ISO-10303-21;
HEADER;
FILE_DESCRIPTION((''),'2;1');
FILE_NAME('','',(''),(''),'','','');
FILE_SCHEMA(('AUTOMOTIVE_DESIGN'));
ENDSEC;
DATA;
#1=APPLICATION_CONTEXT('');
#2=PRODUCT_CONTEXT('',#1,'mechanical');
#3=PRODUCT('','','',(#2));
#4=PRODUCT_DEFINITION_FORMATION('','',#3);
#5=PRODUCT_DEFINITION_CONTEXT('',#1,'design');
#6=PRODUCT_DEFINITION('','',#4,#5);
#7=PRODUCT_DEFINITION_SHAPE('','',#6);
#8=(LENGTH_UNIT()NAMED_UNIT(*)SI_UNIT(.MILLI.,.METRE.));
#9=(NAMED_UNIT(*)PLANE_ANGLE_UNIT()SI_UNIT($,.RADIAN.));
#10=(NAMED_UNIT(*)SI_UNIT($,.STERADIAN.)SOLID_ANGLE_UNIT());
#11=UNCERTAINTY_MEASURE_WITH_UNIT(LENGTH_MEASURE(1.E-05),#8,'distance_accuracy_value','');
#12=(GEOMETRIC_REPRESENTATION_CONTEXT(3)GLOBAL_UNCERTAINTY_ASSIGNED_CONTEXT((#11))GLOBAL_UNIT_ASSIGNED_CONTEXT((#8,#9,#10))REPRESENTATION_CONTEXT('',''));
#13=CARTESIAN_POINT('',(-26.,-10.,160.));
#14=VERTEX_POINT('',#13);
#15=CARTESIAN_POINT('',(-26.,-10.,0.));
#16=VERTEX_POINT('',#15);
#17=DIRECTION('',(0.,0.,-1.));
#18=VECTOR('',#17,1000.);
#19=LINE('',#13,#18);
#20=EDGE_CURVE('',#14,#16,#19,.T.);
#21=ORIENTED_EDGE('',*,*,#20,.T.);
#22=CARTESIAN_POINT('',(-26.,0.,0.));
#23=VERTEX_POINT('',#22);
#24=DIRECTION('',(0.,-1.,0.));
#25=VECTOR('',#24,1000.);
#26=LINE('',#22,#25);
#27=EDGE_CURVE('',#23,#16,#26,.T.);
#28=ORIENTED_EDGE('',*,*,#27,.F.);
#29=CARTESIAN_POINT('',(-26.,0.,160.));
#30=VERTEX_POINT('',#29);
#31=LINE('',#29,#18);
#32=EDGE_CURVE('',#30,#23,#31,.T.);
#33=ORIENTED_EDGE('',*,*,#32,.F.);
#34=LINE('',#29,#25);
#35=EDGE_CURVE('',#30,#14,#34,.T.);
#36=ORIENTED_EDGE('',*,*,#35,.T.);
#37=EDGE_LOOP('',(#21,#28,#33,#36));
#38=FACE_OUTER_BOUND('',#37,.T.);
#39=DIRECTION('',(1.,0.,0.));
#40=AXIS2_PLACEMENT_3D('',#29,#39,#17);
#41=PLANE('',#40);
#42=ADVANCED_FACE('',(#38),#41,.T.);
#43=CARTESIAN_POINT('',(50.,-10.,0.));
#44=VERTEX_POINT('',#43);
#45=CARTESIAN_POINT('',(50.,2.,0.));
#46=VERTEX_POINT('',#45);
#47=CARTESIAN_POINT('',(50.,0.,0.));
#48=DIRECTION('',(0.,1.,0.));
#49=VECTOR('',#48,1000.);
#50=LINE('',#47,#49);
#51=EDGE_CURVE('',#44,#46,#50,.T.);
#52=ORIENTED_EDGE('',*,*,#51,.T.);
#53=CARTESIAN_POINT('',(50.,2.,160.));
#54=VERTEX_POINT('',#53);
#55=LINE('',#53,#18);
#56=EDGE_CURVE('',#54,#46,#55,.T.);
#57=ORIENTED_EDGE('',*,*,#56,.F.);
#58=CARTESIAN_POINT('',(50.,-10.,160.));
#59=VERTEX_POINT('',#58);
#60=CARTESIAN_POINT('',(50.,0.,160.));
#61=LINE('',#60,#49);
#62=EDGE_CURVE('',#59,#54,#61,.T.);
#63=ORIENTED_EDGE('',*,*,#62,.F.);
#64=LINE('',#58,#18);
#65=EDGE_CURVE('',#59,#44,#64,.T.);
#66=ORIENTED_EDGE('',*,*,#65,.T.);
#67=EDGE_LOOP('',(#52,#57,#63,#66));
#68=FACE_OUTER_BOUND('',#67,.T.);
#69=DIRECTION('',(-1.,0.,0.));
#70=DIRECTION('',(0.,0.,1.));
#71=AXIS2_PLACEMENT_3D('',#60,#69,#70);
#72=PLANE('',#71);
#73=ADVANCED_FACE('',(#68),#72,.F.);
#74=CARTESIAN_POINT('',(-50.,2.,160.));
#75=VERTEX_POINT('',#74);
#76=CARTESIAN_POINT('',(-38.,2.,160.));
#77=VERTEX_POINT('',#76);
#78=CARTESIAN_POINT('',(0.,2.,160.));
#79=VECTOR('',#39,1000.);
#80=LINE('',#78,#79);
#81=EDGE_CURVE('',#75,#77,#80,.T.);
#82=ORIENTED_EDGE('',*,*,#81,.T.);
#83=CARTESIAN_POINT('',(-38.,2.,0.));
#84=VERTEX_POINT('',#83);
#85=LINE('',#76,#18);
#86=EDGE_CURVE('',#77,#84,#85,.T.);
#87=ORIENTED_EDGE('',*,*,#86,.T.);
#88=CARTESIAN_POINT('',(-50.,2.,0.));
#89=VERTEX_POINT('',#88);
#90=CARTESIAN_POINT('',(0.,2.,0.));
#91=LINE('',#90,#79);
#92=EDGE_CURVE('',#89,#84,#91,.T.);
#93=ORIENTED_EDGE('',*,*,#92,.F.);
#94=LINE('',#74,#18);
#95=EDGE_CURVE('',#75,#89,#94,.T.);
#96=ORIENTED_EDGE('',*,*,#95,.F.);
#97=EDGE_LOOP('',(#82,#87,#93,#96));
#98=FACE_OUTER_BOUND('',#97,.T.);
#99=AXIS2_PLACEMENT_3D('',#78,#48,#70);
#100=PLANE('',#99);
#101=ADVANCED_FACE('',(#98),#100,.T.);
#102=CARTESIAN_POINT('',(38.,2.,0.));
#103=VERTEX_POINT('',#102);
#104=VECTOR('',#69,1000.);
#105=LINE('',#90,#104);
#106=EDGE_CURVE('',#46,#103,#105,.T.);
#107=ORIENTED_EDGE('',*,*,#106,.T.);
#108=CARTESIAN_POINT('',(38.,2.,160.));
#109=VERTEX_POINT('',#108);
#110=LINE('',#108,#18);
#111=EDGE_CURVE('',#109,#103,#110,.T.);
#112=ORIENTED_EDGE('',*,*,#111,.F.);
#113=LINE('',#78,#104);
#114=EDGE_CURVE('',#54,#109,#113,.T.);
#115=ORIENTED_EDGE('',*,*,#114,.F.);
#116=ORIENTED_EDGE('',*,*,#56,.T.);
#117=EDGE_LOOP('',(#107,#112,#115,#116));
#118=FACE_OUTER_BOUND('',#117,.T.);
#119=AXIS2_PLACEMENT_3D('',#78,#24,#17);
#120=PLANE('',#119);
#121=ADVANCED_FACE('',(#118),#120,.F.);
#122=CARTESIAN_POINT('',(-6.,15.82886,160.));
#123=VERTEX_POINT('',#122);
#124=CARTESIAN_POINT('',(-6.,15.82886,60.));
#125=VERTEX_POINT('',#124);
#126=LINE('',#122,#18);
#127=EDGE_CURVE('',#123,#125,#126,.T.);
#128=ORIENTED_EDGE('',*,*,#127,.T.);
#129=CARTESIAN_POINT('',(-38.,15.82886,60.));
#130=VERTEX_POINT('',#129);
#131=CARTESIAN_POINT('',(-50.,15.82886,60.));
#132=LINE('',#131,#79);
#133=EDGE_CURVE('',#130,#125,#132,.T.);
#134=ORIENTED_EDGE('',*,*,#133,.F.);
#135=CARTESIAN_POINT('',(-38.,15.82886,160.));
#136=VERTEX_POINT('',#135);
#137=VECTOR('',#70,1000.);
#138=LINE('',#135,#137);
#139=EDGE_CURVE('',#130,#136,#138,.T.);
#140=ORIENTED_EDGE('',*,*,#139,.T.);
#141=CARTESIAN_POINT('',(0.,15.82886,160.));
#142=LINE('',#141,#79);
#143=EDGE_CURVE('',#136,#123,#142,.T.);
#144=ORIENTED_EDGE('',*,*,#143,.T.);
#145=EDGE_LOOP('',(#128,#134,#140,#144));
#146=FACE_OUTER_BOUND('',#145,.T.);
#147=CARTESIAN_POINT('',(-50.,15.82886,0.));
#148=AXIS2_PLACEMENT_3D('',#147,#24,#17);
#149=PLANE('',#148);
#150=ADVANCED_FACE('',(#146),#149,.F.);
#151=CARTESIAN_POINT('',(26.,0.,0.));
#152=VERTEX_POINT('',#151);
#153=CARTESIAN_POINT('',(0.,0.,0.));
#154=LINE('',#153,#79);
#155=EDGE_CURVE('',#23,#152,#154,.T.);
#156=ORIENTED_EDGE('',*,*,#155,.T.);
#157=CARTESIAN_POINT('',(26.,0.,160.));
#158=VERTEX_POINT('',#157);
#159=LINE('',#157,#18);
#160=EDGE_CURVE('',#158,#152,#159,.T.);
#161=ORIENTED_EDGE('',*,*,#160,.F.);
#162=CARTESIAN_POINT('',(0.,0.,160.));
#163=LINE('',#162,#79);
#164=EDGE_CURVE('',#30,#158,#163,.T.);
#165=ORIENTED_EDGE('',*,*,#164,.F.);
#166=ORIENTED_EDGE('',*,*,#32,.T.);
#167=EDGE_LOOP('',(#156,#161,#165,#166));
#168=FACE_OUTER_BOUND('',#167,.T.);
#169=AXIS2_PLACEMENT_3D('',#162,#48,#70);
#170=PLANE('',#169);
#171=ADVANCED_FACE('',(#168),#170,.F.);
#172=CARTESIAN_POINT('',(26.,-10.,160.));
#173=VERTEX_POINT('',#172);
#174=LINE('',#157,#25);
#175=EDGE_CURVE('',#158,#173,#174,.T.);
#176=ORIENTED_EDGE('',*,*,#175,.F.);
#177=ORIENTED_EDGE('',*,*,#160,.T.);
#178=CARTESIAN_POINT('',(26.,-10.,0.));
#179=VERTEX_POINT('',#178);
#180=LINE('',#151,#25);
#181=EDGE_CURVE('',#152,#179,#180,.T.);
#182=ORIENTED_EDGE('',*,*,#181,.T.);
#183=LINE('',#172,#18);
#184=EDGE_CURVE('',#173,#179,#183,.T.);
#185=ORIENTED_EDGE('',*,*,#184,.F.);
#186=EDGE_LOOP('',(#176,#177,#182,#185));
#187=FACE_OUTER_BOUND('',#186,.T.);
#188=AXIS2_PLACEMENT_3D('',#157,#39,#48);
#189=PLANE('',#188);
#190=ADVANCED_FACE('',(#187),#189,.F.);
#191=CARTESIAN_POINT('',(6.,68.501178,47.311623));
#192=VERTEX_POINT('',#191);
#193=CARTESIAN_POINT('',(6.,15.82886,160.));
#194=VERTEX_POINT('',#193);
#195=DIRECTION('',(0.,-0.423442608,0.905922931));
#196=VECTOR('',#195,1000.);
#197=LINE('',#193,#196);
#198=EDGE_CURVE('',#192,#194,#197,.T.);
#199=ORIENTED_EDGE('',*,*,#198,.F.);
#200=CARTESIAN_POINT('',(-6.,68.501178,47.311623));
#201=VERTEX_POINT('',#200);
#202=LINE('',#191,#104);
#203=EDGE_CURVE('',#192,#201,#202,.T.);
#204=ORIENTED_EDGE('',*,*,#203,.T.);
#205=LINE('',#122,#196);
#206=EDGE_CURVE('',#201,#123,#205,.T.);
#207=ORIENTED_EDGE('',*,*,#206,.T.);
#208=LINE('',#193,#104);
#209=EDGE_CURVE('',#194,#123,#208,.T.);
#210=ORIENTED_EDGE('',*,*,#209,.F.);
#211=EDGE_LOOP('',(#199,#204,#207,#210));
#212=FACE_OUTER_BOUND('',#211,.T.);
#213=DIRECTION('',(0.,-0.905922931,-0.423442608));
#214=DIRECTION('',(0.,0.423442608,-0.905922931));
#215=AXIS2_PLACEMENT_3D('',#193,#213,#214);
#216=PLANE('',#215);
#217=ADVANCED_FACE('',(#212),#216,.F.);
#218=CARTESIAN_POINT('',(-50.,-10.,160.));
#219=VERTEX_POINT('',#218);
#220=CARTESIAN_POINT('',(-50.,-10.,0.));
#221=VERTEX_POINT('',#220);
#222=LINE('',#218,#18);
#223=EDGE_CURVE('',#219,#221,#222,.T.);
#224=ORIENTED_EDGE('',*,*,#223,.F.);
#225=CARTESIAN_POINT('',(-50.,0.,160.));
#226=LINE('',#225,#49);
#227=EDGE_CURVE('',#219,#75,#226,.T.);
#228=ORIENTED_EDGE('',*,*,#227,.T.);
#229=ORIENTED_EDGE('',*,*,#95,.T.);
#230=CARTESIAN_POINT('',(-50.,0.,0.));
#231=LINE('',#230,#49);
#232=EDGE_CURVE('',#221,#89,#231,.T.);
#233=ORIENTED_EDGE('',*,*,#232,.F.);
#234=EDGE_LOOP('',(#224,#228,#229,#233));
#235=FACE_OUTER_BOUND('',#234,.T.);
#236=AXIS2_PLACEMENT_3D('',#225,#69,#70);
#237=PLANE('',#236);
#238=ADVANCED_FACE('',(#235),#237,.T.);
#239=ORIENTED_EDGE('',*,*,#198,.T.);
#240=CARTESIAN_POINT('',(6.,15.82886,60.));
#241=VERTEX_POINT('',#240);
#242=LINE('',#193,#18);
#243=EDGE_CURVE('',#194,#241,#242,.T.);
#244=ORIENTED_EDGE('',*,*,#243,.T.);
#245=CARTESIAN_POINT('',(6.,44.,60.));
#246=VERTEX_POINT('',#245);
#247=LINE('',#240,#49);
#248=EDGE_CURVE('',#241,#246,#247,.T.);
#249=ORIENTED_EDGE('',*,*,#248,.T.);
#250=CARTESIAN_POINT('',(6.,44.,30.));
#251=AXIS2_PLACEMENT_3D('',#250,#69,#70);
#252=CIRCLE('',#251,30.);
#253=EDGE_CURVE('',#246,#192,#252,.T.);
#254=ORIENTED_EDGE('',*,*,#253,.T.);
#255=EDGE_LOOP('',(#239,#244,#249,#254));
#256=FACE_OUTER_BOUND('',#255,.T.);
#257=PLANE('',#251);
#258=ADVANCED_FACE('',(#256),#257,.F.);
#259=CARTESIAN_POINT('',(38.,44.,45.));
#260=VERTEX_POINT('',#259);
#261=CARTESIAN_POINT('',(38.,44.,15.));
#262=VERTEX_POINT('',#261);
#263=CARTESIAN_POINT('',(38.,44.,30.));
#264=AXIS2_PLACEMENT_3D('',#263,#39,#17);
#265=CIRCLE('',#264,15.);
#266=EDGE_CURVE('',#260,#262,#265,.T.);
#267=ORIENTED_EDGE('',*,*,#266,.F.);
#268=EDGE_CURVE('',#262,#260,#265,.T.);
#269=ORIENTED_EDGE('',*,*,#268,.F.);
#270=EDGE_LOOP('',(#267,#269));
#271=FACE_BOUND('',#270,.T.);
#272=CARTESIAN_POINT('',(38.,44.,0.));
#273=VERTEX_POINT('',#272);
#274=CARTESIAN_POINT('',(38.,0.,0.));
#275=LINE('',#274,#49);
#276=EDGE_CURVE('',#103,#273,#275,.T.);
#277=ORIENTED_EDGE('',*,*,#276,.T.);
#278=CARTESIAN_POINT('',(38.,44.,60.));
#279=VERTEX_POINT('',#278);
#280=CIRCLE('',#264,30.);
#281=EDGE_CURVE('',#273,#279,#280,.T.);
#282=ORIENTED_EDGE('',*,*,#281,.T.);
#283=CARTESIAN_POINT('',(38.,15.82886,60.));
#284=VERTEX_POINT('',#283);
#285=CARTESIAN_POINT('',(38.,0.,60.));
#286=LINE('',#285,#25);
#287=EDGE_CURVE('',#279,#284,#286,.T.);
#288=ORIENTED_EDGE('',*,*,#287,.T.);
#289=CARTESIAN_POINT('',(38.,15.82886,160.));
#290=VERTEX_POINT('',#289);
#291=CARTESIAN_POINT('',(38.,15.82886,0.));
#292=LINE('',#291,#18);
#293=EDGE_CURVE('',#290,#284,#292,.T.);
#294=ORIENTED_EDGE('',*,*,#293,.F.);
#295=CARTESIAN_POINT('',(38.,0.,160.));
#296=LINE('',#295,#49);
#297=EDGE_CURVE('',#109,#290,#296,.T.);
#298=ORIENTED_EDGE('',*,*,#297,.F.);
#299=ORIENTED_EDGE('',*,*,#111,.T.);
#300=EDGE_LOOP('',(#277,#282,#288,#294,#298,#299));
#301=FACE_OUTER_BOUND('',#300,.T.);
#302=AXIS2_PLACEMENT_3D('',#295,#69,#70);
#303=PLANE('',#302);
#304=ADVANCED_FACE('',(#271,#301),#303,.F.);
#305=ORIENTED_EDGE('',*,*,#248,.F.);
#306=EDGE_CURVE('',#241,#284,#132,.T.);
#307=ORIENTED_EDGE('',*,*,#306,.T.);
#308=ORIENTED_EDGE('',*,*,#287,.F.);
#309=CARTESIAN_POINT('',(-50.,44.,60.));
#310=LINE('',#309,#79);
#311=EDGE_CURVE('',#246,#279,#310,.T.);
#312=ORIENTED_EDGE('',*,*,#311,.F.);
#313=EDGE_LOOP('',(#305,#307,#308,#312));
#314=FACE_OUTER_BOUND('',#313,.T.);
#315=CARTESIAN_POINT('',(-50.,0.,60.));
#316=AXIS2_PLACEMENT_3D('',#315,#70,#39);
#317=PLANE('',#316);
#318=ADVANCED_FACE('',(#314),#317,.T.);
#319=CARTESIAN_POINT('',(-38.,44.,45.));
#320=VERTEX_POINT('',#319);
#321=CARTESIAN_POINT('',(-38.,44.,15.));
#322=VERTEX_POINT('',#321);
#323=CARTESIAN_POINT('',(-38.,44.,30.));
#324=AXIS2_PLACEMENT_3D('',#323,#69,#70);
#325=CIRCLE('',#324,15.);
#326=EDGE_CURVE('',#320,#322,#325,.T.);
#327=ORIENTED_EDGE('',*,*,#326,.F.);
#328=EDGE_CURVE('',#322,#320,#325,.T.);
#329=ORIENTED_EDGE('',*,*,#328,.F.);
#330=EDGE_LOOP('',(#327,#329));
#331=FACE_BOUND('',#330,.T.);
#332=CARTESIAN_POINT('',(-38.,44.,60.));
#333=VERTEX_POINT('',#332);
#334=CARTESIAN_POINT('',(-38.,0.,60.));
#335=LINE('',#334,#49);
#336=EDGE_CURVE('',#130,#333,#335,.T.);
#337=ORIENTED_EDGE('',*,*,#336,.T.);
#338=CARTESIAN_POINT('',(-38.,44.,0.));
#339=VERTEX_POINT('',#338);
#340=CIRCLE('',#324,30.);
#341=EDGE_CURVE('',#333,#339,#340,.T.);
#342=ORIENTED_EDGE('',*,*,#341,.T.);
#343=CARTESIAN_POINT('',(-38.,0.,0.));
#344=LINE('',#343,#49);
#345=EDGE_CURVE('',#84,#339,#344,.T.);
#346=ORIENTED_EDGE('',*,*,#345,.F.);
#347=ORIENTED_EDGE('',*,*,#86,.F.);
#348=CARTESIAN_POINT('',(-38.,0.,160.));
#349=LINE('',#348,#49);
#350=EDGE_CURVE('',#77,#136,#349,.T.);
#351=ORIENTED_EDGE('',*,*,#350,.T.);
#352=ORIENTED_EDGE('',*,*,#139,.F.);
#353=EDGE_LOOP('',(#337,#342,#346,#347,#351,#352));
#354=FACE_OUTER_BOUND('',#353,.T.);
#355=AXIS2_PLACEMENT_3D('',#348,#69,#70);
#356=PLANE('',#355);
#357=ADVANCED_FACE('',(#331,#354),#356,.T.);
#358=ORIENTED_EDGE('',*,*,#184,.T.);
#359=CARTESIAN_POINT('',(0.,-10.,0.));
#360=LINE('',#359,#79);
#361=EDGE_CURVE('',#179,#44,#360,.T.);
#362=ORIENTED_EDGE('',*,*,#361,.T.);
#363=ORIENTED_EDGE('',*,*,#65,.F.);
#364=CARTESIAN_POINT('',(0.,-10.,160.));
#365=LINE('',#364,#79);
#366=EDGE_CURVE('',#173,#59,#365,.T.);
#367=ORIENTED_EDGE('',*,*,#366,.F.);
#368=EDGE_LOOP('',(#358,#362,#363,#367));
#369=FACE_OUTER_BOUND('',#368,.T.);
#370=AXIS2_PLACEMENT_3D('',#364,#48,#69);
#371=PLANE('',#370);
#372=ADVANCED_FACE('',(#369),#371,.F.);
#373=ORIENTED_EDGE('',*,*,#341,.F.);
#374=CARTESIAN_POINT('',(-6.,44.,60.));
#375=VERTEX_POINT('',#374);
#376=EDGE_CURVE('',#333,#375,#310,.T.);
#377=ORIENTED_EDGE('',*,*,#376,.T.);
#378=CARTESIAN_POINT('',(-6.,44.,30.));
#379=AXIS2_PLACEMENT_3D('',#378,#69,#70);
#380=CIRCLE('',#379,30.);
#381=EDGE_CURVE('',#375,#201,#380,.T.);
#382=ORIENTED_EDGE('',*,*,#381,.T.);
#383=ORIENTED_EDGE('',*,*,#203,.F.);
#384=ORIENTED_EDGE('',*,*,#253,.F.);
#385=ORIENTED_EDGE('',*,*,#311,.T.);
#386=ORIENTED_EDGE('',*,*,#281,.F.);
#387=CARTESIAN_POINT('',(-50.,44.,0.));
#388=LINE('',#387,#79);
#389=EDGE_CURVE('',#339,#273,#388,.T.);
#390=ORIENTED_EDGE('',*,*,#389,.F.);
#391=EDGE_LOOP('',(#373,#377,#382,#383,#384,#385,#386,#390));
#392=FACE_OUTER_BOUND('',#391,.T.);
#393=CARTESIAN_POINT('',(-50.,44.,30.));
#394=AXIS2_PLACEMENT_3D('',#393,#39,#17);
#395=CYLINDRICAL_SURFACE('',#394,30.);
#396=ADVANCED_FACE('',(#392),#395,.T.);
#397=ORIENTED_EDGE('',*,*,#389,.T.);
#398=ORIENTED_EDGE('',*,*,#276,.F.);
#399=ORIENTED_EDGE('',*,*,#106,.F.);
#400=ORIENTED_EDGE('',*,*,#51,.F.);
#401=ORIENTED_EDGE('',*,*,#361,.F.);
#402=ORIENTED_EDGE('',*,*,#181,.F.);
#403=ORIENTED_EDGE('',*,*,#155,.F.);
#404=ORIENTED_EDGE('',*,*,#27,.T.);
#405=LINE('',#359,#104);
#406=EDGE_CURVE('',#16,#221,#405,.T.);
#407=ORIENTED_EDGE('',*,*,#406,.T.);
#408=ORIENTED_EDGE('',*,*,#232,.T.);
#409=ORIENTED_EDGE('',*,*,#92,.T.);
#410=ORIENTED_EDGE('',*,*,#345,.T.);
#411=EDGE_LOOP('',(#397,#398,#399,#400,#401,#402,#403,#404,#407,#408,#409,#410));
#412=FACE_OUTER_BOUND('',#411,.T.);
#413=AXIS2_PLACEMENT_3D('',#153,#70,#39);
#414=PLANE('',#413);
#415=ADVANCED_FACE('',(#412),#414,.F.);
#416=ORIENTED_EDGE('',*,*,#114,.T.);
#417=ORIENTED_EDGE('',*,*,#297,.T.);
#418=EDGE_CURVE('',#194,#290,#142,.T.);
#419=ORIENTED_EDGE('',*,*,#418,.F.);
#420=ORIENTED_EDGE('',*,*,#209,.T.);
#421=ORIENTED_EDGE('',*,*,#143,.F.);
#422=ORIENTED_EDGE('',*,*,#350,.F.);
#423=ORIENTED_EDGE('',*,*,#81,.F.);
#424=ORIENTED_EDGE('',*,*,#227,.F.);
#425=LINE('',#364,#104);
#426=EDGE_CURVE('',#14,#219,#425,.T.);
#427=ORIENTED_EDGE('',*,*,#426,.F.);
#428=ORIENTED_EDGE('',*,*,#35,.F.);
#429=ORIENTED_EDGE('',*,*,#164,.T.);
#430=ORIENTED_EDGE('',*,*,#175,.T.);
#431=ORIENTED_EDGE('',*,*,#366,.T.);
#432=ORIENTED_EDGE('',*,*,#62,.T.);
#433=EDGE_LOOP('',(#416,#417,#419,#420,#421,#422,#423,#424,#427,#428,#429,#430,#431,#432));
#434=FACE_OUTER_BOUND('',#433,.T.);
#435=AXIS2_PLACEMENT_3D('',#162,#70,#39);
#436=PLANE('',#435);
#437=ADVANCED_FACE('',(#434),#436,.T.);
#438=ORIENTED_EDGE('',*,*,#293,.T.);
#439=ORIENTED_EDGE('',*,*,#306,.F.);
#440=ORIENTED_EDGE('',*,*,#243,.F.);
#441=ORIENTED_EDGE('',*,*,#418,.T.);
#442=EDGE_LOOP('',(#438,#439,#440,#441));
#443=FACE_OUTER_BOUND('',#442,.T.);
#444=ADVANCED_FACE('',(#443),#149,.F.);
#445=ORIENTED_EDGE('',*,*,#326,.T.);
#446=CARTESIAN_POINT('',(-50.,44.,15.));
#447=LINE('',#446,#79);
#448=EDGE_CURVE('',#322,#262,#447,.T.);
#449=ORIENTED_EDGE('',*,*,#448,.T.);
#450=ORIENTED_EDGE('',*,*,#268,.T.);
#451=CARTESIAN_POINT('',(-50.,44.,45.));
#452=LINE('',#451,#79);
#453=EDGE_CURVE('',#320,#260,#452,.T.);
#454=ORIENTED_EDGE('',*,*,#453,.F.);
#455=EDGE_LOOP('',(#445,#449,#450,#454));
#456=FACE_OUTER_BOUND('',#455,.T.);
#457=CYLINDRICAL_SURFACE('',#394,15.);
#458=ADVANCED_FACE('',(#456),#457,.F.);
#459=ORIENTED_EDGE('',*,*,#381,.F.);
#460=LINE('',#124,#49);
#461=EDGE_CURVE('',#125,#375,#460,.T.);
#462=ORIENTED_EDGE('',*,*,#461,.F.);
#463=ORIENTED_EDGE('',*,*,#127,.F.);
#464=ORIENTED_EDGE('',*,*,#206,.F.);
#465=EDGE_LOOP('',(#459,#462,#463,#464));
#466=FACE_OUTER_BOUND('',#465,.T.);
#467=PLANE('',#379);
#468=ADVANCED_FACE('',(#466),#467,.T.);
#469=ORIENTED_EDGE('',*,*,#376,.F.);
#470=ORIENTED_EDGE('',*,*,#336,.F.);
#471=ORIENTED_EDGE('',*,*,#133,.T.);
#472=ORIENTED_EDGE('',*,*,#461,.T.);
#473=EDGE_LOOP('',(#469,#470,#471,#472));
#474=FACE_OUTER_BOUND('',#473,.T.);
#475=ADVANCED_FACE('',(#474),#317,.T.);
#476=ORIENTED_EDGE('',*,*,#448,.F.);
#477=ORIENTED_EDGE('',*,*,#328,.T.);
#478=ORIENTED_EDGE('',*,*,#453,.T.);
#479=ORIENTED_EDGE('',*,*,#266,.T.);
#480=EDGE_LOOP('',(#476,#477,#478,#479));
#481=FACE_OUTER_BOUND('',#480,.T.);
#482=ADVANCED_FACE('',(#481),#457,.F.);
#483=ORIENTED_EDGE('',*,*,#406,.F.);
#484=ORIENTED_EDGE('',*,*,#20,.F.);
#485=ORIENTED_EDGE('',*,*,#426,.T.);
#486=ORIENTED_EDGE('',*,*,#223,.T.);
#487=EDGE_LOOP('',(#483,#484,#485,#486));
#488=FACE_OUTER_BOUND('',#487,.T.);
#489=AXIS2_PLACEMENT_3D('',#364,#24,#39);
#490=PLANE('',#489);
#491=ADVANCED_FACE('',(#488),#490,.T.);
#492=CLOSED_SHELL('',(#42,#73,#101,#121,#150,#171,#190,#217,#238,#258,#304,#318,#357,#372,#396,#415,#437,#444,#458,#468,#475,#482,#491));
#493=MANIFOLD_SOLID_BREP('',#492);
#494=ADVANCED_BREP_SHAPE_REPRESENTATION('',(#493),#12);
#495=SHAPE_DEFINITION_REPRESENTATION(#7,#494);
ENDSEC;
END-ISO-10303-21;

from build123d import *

# Parameters (mm, degrees)
BASE_SLIDE_PROFILE_SKETCH_W     = 76
BASE_SLIDE_PROFILE_SKETCH_H     = 60
BASE_BLOCK_160_DEPTH            = 160
BEARING_BLOCK_SHAPING_CUT_DEPTH = 198.027916804
SUPPORT_RIB_12_DEPTH            = 6
BORE_SKETCH_R                   = 15
BORE_30_DEPTH                   = 198.027916804


with BuildPart() as part:
    # Base Slide Profile Sketch → Base Block 160 (new body)
    with BuildSketch(Plane.XY):
        Polygon((-26, -10), (-26, 0), (26, 0), (26, -10), (50, -10), (50, 2), (38, 2), (38, 14), (-38, 14), (-38, 2), (-50, 2), (-50, -10), align=None)
        with Locations((0, 44)):
            Rectangle(BASE_SLIDE_PROFILE_SKETCH_W, BASE_SLIDE_PROFILE_SKETCH_H)
    extrude(amount=BASE_BLOCK_160_DEPTH)

    # Bearing Block Outline Sketch → Bearing Block Shaping Cut (cut, through all)
    with BuildSketch(Plane(origin=(38, 0, 0), x_dir=(0, 0, -1), z_dir=(1, 0, 0))):
        with BuildLine():
            Line((-60, 15.828860139), (-60, 44))
            ThreePointArc((-60, 44), (-51.213203403, 65.213203468), (-29.999999908, 74))
            Line((-29.999999908, 74), (-160, 74))
            Line((-160, 74), (-160, 15.828860139))
            Line((-160, 15.828860139), (-60, 15.828860139))
        make_face()
        with BuildLine():
            Line((0, 74), (-29.999999908, 74))
            ThreePointArc((-29.999999908, 74), (-8.786796532, 65.213203403), (0, 44))
            Line((0, 44), (0, 74))
        make_face()
    extrude(amount=-BEARING_BLOCK_SHAPING_CUT_DEPTH, mode=Mode.SUBTRACT)

    # Support Rib Sketch → Support Rib 12 (add, symmetric)
    with BuildSketch(Plane(origin=(0, 0, 0), x_dir=(0, 0, -1), z_dir=(1, 0, 0))):
        with BuildLine():
            Line((-160, 15.828860139), (-47.311623158, 68.501177597))
            ThreePointArc((-47.311623158, 68.501177597), (-56.639713725, 57.795856357), (-60, 44))
            Line((-60, 44), (-60, 15.828860139))
            Line((-60, 15.828860139), (-160, 15.828860139))
        make_face()
    extrude(amount=SUPPORT_RIB_12_DEPTH, both=True)

    # Bore Sketch → Bore Ø30 (cut, through all)
    with BuildSketch(Plane(origin=(38, 0, 0), x_dir=(0, 0, -1), z_dir=(1, 0, 0))):
        with Locations((-30, 44)):
            Circle(BORE_SKETCH_R)
    extrude(amount=-BORE_30_DEPTH, mode=Mode.SUBTRACT)


solid = part.part
